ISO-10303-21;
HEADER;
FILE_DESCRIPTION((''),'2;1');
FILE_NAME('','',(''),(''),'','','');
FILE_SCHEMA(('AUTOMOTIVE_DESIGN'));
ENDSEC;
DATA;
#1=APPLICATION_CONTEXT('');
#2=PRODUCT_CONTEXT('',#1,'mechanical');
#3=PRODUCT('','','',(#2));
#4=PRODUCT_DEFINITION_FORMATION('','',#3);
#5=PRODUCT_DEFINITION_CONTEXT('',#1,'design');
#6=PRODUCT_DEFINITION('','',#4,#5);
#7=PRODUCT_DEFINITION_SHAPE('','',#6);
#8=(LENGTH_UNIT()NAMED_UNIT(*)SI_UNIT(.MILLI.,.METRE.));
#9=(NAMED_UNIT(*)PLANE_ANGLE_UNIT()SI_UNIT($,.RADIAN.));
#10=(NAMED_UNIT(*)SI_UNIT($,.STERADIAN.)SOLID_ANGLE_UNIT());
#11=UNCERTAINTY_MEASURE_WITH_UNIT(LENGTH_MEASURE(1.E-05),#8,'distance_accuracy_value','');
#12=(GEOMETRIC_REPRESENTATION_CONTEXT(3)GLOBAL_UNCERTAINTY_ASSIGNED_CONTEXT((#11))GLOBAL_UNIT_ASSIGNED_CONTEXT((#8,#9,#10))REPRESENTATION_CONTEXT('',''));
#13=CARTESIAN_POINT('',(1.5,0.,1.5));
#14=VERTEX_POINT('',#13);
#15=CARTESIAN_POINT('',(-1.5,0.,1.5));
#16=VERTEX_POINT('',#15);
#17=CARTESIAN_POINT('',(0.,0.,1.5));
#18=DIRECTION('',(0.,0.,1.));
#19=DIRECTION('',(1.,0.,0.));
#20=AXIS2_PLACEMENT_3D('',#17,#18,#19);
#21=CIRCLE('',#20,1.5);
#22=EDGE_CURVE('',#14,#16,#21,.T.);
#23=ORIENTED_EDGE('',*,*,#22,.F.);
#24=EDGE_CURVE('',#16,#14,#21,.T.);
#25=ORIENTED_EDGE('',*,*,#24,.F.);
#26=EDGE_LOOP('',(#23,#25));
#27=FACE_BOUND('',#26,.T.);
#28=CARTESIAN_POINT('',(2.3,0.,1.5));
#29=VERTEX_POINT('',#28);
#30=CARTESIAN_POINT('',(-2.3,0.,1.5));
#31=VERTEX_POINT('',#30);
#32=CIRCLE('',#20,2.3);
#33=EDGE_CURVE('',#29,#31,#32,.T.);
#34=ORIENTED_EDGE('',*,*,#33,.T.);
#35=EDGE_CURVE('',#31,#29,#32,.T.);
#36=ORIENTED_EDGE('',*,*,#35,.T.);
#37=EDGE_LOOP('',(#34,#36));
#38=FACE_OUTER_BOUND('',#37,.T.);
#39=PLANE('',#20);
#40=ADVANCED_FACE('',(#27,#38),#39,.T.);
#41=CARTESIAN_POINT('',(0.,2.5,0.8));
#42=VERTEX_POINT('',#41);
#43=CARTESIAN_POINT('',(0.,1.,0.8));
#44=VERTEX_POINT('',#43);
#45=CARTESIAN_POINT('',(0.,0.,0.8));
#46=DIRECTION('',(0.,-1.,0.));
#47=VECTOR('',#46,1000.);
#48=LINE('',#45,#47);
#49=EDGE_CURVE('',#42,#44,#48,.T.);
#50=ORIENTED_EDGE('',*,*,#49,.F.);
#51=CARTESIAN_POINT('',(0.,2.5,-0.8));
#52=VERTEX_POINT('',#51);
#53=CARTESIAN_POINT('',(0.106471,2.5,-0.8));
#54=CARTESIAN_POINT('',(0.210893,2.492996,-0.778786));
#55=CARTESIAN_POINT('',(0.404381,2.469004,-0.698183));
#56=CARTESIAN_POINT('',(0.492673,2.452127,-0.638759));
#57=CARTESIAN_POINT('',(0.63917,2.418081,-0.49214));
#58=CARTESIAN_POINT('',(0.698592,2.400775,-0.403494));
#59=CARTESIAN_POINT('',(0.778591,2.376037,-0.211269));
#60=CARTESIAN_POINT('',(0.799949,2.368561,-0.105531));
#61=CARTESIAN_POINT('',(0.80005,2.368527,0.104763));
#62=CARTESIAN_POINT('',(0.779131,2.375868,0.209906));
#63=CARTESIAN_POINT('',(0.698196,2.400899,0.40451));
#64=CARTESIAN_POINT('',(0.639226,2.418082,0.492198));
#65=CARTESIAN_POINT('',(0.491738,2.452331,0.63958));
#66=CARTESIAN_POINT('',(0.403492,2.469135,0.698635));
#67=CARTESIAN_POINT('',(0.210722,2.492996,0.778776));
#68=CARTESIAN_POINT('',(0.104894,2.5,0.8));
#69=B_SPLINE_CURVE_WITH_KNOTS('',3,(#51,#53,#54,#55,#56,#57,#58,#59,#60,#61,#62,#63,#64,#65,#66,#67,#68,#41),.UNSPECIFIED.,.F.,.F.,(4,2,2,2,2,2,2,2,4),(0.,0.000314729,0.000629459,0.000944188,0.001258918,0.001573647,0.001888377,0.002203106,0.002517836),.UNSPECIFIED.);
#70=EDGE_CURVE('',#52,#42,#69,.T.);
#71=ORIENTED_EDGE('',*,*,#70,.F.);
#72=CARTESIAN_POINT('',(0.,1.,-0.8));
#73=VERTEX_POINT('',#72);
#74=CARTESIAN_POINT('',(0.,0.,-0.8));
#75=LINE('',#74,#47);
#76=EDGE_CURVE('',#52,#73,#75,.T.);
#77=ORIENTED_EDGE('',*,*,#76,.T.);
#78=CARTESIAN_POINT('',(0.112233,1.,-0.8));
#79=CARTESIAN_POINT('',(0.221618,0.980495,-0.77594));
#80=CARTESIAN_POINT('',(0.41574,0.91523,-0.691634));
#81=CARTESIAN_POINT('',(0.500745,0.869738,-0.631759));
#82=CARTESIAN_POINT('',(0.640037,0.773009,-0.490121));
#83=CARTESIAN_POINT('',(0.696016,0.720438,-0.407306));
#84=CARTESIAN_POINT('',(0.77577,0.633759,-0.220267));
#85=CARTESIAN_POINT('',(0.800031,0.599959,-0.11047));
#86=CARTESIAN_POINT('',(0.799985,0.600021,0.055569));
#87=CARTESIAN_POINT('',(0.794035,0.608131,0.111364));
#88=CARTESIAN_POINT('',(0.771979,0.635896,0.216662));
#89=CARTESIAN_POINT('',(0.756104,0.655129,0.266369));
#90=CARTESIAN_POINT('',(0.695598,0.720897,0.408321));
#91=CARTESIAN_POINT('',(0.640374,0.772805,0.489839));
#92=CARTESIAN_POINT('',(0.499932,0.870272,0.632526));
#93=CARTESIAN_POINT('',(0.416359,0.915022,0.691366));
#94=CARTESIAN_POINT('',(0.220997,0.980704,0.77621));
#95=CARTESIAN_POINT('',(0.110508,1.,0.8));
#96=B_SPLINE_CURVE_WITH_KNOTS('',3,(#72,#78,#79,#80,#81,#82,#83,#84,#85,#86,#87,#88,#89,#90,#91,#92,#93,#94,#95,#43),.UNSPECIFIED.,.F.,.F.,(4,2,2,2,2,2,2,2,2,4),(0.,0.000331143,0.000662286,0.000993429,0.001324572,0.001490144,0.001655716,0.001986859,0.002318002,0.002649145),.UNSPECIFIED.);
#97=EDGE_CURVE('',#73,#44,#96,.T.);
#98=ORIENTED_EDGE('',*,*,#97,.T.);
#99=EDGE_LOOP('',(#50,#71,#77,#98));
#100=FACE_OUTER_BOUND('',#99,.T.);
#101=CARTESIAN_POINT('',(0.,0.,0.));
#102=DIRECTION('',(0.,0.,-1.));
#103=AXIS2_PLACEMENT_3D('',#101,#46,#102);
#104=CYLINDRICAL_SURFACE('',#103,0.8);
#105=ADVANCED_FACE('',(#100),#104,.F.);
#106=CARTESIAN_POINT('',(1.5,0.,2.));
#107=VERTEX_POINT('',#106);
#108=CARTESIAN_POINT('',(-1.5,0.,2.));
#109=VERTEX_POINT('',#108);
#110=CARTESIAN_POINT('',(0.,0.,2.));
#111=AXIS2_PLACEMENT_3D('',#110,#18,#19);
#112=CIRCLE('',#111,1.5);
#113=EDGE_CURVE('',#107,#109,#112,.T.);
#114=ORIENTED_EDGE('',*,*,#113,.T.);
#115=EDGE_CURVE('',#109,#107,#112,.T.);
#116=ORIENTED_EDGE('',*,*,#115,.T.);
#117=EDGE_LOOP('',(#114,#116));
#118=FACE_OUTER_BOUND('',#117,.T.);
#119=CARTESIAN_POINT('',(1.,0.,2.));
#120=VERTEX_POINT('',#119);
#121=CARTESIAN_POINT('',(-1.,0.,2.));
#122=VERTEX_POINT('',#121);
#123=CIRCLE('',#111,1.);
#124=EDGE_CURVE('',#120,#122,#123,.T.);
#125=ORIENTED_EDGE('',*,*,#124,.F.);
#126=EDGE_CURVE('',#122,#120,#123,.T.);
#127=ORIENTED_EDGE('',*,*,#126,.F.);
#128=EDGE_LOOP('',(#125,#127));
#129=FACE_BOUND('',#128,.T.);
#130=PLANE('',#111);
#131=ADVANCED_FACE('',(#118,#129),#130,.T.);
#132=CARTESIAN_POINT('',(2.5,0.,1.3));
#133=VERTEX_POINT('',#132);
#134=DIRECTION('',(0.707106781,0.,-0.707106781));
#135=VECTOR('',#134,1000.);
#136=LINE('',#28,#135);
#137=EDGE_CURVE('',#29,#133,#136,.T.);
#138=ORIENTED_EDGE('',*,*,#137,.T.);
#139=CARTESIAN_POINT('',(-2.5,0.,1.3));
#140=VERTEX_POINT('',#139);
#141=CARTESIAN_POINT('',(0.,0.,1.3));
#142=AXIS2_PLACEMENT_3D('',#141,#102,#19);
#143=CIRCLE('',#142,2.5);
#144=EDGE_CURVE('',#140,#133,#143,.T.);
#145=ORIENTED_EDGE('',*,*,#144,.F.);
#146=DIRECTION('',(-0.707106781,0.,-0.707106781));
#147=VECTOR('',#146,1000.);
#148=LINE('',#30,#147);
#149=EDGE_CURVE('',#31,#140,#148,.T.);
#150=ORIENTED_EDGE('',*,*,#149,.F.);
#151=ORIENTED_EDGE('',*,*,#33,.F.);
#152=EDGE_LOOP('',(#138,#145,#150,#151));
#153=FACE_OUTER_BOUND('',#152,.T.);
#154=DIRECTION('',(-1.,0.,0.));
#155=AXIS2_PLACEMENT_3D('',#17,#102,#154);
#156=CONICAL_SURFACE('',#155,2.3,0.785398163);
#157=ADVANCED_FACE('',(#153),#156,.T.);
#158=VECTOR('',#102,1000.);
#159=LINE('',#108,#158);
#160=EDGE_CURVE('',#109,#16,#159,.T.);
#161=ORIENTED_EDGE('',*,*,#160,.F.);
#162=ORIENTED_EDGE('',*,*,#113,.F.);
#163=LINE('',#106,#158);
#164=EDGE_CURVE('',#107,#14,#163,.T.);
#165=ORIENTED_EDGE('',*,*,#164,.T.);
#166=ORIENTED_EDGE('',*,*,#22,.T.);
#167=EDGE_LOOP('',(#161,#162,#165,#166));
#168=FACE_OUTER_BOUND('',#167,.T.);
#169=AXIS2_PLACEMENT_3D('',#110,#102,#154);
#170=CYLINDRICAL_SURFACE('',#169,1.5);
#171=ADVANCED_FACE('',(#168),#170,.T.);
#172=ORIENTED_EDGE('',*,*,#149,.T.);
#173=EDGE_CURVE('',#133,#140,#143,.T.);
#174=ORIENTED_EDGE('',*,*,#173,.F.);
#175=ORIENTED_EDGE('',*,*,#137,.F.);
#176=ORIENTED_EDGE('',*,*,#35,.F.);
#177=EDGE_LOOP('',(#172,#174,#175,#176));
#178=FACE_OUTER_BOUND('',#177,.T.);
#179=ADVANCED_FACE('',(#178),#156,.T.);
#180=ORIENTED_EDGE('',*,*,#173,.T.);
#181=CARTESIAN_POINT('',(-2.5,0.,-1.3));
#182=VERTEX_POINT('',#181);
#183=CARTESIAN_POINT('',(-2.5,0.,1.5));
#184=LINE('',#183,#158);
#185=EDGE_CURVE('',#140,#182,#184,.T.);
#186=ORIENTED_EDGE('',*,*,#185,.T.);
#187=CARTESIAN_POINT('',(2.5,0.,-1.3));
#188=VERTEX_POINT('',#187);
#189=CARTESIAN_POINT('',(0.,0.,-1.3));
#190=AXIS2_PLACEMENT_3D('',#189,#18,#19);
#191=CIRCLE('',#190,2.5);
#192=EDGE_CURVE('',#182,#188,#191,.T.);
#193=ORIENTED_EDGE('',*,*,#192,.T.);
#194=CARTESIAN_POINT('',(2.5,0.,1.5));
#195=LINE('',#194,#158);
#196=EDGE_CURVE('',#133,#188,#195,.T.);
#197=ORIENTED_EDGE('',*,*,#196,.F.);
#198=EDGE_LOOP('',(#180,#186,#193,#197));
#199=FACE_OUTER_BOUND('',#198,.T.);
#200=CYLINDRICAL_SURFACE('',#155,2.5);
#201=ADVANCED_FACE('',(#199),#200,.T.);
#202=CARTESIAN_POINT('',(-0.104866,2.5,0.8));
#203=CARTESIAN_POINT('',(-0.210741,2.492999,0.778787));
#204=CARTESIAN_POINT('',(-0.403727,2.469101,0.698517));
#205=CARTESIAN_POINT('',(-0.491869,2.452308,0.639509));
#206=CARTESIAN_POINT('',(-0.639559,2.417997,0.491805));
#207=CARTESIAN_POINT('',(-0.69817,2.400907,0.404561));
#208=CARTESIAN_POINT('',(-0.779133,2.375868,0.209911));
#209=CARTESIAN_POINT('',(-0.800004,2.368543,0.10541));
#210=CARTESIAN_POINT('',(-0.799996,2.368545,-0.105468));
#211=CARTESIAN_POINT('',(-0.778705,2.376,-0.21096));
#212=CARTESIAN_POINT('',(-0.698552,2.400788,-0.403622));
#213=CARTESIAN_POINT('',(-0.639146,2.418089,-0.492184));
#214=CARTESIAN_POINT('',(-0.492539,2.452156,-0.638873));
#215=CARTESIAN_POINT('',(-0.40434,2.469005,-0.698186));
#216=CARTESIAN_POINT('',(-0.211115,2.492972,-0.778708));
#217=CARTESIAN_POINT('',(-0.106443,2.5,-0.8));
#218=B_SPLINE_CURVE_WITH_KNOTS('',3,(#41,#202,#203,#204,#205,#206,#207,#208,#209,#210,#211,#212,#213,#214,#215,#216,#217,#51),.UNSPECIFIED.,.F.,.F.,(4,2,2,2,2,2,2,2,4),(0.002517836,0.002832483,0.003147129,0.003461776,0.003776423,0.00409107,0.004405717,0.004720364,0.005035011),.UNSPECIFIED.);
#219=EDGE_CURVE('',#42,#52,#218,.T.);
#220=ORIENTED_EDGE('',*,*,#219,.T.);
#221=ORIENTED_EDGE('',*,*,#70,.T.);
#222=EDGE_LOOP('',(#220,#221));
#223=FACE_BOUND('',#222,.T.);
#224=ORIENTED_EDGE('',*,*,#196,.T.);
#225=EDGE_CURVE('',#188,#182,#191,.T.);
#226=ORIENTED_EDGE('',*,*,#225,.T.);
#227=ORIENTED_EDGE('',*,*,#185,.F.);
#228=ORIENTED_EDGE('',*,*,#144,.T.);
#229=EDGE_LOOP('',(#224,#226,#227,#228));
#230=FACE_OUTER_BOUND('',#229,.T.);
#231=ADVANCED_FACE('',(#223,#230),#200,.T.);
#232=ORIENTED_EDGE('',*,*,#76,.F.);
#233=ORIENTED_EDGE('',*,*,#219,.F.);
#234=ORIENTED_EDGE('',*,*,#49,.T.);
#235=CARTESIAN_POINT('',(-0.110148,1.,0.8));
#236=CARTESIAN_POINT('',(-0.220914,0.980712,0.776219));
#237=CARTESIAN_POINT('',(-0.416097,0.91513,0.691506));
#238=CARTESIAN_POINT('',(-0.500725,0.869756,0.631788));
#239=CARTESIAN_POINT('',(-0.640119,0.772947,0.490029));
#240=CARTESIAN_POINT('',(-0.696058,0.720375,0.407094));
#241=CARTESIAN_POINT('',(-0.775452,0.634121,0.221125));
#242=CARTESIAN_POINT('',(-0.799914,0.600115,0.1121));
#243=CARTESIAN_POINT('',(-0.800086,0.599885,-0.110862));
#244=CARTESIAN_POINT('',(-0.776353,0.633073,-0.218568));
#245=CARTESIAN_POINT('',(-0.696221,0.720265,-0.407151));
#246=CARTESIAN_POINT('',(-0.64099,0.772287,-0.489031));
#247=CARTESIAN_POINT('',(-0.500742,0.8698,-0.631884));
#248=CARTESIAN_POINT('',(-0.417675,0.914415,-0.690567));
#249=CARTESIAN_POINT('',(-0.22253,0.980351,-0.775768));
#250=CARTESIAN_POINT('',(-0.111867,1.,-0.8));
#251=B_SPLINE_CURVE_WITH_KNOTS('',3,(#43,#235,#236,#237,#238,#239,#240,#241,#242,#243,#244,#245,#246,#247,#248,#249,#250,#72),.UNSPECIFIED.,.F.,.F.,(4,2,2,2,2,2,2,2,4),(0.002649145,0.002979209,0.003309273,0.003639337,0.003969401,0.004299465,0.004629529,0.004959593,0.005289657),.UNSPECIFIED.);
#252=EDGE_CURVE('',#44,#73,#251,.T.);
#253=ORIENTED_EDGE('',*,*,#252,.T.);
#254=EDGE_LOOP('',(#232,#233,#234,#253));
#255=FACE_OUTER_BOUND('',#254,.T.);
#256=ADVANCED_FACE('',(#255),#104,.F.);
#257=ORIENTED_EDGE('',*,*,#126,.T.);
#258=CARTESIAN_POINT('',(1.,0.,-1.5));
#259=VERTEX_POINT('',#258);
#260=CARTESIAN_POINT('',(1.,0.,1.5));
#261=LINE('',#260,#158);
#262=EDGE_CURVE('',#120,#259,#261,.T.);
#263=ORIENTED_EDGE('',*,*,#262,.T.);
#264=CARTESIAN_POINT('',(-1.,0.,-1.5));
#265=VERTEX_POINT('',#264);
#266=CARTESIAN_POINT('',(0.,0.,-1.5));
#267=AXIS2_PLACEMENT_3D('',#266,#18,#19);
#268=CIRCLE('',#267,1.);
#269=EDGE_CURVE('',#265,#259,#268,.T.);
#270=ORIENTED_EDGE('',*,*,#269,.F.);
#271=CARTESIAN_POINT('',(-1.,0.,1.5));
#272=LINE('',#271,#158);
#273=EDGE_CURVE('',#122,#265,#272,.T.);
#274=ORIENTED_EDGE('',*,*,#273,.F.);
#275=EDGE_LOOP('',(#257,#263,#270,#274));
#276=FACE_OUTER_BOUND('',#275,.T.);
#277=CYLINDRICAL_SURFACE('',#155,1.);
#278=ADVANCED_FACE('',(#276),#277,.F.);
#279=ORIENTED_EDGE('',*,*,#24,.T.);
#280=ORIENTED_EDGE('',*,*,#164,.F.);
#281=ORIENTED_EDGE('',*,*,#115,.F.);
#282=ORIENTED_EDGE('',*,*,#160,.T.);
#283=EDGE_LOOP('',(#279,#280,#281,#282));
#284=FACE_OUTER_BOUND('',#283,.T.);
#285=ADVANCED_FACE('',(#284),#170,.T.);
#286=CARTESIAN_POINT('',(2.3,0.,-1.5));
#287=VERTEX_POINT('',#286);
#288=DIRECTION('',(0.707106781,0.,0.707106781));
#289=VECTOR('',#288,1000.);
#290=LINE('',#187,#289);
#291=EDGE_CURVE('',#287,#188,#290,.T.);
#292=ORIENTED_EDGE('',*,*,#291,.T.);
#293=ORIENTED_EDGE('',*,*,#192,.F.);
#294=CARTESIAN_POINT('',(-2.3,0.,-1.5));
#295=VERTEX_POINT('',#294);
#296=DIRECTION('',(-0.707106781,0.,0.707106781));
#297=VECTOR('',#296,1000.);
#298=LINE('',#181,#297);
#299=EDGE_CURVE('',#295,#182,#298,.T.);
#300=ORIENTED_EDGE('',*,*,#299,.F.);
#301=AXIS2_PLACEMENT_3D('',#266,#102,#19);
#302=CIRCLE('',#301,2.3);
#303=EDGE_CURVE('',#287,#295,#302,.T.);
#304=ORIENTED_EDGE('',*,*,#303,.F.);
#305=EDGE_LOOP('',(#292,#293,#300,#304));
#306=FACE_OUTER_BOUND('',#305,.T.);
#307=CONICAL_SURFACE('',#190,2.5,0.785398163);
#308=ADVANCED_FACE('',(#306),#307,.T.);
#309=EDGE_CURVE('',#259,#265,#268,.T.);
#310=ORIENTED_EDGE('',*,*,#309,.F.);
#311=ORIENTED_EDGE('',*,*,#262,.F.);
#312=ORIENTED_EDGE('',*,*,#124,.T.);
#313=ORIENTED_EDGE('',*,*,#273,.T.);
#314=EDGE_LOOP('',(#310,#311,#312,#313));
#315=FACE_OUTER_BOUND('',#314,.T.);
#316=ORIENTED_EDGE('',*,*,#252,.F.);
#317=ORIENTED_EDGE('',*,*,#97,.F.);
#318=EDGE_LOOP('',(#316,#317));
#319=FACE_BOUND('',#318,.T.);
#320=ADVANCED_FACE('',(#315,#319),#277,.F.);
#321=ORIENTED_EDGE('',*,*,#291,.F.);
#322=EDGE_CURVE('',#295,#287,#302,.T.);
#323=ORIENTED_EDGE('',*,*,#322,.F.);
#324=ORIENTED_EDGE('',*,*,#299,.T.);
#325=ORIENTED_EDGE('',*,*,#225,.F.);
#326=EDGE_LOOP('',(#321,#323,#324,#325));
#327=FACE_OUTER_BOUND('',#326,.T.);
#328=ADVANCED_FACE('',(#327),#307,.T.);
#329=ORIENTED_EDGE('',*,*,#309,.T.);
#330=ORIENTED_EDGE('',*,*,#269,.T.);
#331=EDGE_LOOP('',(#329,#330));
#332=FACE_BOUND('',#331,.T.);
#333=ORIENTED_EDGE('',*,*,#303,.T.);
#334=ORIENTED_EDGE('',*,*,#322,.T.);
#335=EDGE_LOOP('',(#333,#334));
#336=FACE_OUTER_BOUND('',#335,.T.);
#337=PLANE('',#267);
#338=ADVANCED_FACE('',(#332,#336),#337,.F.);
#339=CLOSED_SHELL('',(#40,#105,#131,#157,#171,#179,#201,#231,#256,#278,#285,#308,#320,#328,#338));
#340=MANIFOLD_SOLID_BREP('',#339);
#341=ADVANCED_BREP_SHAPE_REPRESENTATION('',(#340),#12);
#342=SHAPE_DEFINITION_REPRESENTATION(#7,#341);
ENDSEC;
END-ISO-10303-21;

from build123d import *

# Parameters (mm, degrees)
SKETCH1_R           = 2.5
SKETCH1_R_2         = 1
BOSS_EXTRUDE1_DEPTH = 1.5
SKETCH2_R           = 1.5
SKETCH2_R_2         = 1
BOSS_EXTRUDE2_DEPTH = 0.5
SKETCH3_W           = 0.8
SKETCH3_H           = 2.5
CHAMFER1_SIZE       = 0.2


with BuildPart() as part:
    # Sketch1 → Boss-Extrude1 (new, symmetric)
    with BuildSketch(Plane.XY):
        Circle(SKETCH1_R)
        Circle(SKETCH1_R_2, mode=Mode.SUBTRACT)
    extrude(amount=BOSS_EXTRUDE1_DEPTH, both=True)

    # Sketch2 → Boss-Extrude2 (add)
    with BuildSketch(Plane.XY.offset(1.5)):
        Circle(SKETCH2_R)
        Circle(SKETCH2_R_2, mode=Mode.SUBTRACT)
    extrude(amount=BOSS_EXTRUDE2_DEPTH)

    # Sketch3 → M2 Tapped Hole1 (revolve, cut)
    with BuildSketch(Plane(origin=(0, 0, 0), x_dir=(0, 0, -1), z_dir=(1, 0, 0))):
        with Locations((0.4, 1.25)):
            Rectangle(SKETCH3_W, SKETCH3_H)
    revolve(axis=Axis((0, -6.35, 0), (0, 1, 0)), mode=Mode.SUBTRACT)

    # Chamfer1
    chamfer1_edges = [part.edges().sort_by_distance(p)[0] for p in [
        (-2.5, 0, -1.5),
        (-2.5, 0, 1.5),
    ]]
    chamfer(chamfer1_edges, length=CHAMFER1_SIZE)


solid = part.part
